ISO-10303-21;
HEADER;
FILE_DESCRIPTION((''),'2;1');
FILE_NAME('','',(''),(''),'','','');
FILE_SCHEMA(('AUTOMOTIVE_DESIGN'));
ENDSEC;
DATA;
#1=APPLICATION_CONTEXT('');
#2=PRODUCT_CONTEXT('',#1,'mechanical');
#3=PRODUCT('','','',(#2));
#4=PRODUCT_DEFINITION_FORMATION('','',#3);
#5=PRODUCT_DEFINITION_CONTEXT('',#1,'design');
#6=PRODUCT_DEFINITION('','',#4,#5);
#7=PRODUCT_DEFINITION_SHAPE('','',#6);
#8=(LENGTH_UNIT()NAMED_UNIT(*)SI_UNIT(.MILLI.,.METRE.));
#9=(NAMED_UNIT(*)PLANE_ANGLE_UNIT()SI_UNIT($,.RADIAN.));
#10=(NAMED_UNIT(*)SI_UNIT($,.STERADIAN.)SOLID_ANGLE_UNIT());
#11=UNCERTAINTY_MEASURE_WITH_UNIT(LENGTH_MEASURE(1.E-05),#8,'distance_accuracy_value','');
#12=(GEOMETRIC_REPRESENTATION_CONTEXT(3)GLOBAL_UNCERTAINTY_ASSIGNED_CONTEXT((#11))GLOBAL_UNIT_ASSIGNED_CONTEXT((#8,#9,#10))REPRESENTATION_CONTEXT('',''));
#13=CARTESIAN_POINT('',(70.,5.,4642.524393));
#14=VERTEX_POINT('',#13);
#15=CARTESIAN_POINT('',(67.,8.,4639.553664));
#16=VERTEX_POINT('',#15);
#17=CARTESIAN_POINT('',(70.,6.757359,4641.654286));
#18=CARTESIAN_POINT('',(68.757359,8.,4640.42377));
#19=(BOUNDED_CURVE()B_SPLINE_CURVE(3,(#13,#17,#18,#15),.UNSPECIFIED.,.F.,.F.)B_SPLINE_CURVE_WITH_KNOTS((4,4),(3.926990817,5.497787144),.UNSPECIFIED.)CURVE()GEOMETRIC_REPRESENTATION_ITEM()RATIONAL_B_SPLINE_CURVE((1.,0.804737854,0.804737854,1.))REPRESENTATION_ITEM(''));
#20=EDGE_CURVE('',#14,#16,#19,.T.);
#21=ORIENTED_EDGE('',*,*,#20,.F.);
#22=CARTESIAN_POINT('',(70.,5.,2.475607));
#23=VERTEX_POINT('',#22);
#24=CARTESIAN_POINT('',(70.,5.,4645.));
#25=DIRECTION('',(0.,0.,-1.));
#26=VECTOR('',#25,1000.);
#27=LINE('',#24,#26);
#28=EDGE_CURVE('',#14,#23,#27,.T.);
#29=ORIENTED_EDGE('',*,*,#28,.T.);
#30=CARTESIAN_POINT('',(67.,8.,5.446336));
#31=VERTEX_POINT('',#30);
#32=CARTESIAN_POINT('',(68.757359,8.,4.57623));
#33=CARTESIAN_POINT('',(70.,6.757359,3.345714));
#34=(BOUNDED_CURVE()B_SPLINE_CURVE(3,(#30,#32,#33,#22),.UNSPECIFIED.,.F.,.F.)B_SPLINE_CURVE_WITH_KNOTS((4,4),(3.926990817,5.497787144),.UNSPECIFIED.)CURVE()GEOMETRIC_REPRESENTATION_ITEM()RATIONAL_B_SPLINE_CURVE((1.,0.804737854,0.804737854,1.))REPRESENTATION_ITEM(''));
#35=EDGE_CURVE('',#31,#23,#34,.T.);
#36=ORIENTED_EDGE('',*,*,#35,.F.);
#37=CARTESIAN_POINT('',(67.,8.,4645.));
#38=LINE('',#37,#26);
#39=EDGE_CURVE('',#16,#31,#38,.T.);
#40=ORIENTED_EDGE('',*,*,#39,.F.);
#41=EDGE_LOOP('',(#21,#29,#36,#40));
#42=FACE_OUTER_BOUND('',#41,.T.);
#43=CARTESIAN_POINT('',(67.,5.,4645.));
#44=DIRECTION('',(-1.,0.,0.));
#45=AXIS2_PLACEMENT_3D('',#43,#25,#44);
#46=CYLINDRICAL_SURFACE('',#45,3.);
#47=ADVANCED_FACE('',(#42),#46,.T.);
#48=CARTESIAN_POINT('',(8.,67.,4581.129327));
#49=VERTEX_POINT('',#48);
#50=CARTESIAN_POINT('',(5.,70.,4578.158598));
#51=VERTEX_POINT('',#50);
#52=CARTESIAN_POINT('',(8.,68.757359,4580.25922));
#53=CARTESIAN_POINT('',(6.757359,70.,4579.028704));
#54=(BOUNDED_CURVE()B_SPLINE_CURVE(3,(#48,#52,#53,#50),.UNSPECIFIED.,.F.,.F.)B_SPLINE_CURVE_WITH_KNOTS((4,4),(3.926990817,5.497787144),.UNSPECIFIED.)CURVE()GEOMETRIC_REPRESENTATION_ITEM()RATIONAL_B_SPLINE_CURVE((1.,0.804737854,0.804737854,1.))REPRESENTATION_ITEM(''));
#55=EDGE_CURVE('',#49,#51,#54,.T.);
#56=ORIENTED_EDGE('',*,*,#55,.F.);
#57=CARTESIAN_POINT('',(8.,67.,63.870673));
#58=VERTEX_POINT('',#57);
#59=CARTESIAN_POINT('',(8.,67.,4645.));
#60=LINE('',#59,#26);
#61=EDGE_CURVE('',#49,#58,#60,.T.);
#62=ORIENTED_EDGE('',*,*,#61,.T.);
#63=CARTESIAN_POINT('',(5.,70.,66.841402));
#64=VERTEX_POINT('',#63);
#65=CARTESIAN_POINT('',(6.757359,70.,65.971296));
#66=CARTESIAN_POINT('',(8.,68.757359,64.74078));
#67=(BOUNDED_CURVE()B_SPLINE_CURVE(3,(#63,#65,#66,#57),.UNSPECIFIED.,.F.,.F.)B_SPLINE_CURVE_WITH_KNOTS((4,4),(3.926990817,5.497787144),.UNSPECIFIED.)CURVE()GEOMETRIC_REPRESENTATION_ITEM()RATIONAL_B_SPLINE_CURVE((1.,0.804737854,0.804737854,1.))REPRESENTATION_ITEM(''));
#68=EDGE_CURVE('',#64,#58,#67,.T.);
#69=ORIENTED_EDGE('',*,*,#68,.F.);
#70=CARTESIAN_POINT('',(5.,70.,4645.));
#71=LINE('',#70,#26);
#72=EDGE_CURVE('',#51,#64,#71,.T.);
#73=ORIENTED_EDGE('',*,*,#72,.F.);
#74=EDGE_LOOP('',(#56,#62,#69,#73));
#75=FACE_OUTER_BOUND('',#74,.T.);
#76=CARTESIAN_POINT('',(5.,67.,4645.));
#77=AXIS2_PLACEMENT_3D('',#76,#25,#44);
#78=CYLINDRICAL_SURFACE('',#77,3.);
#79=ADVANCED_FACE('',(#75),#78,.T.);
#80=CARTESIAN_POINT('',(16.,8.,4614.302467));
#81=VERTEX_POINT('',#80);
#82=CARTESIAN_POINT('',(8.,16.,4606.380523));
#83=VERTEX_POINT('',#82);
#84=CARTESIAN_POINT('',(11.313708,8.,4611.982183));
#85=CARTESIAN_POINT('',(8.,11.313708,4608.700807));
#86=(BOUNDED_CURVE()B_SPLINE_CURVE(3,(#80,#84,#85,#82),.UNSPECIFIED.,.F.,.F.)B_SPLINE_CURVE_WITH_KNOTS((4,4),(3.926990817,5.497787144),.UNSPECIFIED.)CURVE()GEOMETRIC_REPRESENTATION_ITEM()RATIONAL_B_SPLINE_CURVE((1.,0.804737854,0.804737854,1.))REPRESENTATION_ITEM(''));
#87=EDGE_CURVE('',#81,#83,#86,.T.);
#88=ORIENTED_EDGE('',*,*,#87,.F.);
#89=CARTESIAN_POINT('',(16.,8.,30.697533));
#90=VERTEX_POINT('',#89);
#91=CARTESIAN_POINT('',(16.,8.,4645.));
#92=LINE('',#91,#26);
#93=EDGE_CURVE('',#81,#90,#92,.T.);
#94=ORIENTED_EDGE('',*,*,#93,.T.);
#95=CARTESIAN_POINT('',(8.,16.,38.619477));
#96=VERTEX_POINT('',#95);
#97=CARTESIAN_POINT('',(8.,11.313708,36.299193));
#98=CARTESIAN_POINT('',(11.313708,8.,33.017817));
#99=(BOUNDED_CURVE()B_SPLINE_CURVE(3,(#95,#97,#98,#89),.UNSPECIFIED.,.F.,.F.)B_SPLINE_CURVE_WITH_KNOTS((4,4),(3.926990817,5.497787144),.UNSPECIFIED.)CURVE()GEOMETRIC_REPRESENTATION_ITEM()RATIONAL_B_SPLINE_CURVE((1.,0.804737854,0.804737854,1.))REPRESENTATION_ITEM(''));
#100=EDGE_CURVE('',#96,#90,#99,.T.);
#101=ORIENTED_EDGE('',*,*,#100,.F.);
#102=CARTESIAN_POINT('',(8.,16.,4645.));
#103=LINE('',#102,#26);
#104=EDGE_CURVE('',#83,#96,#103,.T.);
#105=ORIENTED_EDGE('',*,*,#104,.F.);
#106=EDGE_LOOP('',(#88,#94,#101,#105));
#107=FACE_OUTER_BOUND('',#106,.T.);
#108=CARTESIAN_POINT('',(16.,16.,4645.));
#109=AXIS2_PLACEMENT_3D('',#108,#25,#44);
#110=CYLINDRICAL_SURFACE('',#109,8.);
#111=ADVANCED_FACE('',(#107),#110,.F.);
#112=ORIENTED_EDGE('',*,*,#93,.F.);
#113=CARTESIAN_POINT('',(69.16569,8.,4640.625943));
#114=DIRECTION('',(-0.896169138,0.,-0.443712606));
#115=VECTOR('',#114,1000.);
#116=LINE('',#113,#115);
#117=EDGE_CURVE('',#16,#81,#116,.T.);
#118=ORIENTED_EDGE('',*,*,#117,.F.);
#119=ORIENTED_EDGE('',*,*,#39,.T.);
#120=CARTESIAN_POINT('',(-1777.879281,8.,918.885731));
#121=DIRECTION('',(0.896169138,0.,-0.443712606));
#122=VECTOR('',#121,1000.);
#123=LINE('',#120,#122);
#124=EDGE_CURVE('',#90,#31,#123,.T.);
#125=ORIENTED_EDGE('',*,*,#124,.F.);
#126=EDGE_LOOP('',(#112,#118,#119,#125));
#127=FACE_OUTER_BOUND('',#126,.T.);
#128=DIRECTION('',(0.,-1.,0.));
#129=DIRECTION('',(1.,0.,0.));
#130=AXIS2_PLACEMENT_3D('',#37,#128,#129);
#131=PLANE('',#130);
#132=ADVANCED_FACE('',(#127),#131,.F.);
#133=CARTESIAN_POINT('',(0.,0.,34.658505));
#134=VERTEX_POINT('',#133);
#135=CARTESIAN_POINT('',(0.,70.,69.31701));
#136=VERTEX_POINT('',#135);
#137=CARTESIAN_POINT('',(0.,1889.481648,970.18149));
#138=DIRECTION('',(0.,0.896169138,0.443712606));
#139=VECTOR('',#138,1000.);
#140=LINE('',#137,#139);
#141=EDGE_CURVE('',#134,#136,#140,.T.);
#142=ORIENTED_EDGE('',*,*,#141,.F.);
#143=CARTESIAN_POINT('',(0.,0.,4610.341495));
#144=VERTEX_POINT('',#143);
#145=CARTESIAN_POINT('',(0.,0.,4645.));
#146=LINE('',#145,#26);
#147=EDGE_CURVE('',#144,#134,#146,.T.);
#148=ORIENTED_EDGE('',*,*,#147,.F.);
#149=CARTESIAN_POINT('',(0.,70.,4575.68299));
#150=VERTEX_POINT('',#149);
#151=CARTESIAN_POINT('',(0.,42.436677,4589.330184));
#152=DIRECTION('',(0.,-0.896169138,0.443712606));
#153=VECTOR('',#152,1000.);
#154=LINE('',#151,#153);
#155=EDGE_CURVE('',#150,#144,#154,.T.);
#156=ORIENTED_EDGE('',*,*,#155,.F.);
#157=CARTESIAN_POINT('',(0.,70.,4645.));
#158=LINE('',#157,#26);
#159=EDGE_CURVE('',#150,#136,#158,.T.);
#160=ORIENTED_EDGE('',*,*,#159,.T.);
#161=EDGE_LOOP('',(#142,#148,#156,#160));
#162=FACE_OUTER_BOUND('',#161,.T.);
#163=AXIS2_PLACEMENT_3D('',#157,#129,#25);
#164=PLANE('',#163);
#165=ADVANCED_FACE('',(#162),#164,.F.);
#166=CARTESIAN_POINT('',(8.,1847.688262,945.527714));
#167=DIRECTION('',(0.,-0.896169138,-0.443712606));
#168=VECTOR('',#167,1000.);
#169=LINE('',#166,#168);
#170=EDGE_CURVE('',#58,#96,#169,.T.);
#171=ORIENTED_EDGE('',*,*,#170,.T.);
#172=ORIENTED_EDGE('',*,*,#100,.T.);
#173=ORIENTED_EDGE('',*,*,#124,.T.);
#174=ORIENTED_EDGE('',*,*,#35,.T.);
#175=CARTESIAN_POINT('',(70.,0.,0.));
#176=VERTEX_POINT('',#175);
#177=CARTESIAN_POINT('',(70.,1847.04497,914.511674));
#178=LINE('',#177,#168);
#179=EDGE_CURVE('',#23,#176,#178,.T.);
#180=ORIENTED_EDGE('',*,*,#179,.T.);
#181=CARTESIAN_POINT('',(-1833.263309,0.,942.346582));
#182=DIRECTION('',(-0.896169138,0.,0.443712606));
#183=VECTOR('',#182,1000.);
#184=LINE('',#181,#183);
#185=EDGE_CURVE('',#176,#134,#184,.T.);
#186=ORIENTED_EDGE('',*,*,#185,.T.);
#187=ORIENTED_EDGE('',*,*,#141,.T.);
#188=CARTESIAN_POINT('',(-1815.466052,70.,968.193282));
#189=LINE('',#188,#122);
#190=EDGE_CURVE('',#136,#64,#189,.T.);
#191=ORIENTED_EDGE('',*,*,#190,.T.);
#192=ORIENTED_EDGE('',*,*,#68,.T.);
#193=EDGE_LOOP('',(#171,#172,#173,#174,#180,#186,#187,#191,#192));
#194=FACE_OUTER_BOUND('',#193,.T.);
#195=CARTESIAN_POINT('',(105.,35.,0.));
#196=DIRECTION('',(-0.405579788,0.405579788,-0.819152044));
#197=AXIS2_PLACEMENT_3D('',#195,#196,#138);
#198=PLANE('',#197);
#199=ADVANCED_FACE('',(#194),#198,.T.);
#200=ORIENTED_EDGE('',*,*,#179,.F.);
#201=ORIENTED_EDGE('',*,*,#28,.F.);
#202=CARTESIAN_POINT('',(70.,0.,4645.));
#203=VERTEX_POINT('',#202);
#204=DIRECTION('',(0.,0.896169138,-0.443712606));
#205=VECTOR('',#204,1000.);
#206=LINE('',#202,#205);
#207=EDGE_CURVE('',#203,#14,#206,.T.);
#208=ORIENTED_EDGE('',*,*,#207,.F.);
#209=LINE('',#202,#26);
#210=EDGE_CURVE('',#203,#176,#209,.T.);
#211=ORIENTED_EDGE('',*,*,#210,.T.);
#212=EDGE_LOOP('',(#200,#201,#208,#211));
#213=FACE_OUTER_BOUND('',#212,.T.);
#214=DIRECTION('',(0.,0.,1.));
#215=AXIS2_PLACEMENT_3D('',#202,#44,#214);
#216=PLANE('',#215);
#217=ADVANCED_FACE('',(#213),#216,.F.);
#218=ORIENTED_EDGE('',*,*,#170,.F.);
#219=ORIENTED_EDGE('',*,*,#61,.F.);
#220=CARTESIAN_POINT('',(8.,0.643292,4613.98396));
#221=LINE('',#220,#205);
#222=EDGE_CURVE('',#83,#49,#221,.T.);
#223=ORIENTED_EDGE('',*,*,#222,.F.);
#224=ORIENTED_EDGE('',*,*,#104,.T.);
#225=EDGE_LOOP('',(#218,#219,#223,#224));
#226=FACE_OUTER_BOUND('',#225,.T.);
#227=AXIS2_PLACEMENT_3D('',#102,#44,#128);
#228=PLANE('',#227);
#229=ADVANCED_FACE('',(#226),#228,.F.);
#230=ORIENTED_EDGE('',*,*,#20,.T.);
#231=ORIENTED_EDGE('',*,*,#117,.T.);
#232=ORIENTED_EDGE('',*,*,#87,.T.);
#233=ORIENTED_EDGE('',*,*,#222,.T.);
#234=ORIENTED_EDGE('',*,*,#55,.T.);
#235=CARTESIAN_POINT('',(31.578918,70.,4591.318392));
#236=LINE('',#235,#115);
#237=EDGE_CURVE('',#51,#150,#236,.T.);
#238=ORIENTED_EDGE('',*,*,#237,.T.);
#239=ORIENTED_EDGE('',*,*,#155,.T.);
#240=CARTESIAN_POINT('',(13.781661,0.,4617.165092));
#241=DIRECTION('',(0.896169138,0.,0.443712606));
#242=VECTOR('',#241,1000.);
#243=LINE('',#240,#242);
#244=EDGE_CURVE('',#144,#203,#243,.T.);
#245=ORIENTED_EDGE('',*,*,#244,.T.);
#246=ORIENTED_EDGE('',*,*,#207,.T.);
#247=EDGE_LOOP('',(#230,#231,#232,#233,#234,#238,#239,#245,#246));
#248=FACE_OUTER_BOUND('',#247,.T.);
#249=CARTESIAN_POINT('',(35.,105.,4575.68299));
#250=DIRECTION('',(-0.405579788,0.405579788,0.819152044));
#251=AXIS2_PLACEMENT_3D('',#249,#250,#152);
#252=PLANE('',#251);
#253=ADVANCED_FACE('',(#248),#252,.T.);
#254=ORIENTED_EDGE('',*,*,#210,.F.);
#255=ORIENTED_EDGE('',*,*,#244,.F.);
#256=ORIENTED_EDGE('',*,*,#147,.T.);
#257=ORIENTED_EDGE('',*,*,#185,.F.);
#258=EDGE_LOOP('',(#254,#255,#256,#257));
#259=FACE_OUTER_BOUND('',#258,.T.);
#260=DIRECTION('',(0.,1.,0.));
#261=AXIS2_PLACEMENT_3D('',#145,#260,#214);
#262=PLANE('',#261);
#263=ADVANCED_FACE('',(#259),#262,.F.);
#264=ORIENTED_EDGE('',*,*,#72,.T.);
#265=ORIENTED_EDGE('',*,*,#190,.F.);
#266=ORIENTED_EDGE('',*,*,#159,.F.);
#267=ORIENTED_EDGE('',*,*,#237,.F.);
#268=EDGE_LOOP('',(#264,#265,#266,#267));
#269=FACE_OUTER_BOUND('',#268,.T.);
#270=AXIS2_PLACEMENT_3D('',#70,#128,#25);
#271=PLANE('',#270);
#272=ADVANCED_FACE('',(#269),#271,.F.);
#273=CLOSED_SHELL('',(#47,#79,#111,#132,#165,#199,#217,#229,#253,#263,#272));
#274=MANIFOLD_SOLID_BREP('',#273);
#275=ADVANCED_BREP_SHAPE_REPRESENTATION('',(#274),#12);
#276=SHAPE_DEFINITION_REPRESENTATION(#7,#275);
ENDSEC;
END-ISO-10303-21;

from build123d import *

# Parameters (mm, degrees)
BOSS_EXTRUDE1_DEPTH     = 4645
CUT_EXTRUDE4_DEPTH      = 4647.054777981
CUT_EXTRUDE4_DEPTH_BACK = 10


with BuildPart() as part:
    # Sketch1 → Boss-Extrude1 (new body)
    with BuildSketch(Plane.XY):
        with BuildLine():
            Line((0, 70), (0, 0))
            Line((0, 0), (70, 0))
            Line((70, 0), (70, 5))
            ThreePointArc((70, 5), (69.121320344, 7.121320344), (67, 8))
            Line((67, 8), (16, 8))
            ThreePointArc((16, 8), (10.343145751, 10.343145751), (8, 16))
            Line((8, 16), (8, 67))
            ThreePointArc((8, 67), (7.121320344, 69.121320344), (5, 70))
            Line((5, 70), (0, 70))
        make_face()
    extrude(amount=BOSS_EXTRUDE1_DEPTH)

    # Sketch3 → Cut-Extrude4 (cut, two sides: drawn at the far end of the back side and taken through both)
    with BuildSketch(Plane(origin=(0, 0, 0), x_dir=(0, 0, -1), z_dir=(0.7071067811865488, 0.7071067811865464, 0)).offset(-CUT_EXTRUDE4_DEPTH_BACK)):
        Polygon((0, -49.497474683), (-69.317009791, 49.497474683), (0, 49.497474683), align=None)
        Polygon((-4645, -49.497474683), (-4645, 49.497474683), (-4575.682990209, 49.497474683), align=None)
    extrude(amount=CUT_EXTRUDE4_DEPTH + CUT_EXTRUDE4_DEPTH_BACK, mode=Mode.SUBTRACT)


solid = part.part
